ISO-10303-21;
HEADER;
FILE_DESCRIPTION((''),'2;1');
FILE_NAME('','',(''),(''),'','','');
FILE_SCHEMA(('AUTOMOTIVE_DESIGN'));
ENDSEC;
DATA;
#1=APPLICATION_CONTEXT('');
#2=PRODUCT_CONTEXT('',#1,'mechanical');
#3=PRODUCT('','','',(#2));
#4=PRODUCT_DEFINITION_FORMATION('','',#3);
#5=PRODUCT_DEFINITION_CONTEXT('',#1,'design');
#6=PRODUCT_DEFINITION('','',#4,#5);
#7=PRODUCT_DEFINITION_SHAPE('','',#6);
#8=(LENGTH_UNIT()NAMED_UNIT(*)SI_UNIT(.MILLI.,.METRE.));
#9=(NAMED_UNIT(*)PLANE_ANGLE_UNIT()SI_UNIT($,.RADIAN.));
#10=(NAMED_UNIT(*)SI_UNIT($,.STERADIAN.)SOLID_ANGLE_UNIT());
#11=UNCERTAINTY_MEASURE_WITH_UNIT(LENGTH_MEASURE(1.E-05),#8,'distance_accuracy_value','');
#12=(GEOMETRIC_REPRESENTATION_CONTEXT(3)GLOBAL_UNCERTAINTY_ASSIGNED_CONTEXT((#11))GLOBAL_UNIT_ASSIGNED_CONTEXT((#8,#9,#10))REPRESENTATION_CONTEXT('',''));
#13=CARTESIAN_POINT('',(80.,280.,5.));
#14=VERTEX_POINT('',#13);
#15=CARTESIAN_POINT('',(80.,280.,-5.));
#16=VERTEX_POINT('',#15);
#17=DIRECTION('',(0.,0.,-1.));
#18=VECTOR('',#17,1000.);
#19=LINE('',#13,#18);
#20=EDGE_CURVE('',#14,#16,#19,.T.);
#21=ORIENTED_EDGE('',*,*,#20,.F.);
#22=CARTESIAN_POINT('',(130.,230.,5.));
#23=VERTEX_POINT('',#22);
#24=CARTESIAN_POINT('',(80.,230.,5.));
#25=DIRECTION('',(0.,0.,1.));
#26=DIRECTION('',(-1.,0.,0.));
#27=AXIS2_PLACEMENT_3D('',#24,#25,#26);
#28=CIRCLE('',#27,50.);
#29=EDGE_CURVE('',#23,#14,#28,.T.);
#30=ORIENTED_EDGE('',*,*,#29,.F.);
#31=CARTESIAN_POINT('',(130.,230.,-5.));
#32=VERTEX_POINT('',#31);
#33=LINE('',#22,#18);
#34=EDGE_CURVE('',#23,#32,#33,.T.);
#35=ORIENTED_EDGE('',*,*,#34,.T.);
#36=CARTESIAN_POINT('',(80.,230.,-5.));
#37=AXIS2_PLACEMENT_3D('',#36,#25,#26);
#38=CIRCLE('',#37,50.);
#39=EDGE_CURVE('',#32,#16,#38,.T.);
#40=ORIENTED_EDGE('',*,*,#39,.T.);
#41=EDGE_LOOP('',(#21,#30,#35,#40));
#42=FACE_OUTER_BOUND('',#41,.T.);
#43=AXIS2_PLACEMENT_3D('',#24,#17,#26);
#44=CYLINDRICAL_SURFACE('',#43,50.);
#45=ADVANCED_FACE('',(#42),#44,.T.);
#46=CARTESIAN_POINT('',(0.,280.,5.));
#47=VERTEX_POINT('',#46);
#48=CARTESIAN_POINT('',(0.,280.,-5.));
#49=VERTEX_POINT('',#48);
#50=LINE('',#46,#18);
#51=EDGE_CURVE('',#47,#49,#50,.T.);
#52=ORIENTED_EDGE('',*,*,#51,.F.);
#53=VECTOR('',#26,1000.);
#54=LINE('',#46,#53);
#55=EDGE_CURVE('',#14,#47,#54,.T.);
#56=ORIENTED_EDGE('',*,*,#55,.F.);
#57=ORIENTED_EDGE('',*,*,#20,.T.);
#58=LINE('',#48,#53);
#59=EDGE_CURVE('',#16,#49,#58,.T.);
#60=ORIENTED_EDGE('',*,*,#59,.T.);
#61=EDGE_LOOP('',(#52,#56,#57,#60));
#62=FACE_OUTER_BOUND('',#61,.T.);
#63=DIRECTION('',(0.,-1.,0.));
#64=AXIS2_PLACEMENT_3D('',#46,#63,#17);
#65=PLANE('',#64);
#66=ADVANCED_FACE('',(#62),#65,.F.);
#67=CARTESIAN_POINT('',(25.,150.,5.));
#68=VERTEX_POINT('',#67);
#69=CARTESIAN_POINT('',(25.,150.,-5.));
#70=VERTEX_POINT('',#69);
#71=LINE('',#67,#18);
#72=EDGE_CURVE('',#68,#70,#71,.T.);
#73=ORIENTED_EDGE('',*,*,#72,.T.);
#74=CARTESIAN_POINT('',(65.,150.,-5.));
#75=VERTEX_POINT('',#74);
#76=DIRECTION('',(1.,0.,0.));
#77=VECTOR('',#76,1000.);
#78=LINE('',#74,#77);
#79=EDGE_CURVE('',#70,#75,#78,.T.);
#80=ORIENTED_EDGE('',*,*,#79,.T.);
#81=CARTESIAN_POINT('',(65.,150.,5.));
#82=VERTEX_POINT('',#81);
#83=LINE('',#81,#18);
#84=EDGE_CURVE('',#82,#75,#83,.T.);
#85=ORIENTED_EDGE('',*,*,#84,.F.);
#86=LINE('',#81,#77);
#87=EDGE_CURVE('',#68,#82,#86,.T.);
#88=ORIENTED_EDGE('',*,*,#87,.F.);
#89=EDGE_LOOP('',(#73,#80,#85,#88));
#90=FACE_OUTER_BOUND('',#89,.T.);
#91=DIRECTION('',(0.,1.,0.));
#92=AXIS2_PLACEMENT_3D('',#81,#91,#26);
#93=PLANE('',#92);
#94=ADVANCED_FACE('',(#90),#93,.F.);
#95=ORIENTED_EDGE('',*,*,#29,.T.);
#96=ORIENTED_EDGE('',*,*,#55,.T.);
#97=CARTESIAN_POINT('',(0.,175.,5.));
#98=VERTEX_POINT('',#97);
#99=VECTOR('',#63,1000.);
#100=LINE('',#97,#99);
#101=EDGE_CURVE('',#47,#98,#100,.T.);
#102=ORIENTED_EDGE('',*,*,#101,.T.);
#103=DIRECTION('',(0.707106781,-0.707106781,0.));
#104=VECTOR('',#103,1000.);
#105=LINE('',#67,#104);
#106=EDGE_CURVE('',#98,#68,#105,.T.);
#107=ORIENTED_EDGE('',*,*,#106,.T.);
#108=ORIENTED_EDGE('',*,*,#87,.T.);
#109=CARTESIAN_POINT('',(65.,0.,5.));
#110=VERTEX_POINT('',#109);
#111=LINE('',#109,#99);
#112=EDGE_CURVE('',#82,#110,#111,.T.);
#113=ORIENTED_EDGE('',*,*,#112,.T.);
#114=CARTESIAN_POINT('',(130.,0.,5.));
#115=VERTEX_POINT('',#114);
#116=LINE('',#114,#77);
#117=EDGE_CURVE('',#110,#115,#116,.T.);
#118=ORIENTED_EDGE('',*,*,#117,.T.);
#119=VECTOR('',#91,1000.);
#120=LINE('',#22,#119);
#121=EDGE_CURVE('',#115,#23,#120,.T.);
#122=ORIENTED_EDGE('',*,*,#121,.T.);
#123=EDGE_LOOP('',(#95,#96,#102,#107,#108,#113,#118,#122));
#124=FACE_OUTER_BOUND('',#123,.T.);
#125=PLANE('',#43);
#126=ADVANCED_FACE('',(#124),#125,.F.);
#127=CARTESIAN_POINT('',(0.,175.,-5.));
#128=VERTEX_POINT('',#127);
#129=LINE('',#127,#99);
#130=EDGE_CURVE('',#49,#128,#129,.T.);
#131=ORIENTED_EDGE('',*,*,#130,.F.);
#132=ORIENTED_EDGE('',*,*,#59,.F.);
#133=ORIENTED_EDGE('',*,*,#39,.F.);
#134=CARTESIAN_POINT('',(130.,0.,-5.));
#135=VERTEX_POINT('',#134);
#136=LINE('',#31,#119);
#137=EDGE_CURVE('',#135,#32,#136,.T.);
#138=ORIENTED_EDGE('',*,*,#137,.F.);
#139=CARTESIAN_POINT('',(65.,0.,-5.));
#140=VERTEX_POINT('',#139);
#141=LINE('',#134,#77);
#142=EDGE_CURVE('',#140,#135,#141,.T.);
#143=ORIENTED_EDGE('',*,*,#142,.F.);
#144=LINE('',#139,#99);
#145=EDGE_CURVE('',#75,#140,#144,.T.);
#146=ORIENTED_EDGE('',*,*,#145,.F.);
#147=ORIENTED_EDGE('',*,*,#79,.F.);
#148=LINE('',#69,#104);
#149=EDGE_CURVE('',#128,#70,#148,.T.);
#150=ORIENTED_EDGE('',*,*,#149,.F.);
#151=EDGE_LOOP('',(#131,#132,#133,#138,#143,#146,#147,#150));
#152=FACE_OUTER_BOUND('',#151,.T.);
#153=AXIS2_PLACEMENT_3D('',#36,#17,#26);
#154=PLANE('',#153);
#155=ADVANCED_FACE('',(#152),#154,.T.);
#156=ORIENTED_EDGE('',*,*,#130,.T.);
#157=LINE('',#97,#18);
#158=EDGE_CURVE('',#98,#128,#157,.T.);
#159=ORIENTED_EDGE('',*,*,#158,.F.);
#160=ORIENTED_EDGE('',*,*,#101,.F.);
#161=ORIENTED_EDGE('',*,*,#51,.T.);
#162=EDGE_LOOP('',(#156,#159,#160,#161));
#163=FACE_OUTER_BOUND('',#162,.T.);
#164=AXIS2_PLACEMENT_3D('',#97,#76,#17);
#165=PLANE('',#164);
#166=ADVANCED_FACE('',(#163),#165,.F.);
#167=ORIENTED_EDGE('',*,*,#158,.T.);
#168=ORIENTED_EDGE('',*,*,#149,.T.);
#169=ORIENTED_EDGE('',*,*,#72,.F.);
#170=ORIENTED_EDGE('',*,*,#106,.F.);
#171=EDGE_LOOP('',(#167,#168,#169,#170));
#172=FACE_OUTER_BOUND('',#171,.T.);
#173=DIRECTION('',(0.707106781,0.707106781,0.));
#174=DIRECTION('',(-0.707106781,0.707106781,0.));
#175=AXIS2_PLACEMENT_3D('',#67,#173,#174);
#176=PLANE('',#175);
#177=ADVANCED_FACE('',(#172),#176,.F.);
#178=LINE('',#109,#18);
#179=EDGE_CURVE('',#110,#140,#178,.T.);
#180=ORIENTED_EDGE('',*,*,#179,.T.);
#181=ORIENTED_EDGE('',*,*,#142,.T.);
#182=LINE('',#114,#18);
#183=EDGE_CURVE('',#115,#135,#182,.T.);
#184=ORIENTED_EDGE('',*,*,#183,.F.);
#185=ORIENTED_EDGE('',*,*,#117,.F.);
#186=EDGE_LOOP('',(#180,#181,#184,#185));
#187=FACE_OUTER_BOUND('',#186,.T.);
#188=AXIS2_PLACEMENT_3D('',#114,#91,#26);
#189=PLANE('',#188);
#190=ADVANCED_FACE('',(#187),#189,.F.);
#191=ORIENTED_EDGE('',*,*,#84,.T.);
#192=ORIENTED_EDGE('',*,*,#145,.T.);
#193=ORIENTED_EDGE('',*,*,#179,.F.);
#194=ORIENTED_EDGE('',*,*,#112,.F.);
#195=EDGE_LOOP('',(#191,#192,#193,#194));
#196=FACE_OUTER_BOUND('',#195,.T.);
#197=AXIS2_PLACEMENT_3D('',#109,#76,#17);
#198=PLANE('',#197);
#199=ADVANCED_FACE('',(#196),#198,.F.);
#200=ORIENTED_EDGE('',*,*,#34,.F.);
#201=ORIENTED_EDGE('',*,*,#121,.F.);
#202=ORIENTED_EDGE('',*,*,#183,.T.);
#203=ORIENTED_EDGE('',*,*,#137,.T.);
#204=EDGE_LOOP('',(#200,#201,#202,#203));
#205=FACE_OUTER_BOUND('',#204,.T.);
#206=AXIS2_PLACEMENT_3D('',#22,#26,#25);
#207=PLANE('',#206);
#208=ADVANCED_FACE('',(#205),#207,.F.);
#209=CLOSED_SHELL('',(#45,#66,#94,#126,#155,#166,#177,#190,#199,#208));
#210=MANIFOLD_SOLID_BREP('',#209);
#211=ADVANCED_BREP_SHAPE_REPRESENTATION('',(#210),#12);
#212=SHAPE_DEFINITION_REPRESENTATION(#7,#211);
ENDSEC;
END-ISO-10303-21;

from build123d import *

# Parameters (mm, degrees)
BOSS_EXTRUDE1_DEPTH = 5


with BuildPart() as part:
    # Sketch1 → Boss-Extrude1 (new, symmetric)
    with BuildSketch(Plane.XY):
        with BuildLine():
            Line((0, 175), (0, 280))
            Line((0, 280), (80, 280))
            ThreePointArc((80, 280), (115.355339059, 265.355339059), (130, 230))
            Line((130, 230), (130, 0))
            Line((130, 0), (65, 0))
            Line((65, 0), (65, 150))
            Line((65, 150), (25, 150))
            Line((25, 150), (0, 175))
        make_face()
    extrude(amount=BOSS_EXTRUDE1_DEPTH, both=True)


solid = part.part
